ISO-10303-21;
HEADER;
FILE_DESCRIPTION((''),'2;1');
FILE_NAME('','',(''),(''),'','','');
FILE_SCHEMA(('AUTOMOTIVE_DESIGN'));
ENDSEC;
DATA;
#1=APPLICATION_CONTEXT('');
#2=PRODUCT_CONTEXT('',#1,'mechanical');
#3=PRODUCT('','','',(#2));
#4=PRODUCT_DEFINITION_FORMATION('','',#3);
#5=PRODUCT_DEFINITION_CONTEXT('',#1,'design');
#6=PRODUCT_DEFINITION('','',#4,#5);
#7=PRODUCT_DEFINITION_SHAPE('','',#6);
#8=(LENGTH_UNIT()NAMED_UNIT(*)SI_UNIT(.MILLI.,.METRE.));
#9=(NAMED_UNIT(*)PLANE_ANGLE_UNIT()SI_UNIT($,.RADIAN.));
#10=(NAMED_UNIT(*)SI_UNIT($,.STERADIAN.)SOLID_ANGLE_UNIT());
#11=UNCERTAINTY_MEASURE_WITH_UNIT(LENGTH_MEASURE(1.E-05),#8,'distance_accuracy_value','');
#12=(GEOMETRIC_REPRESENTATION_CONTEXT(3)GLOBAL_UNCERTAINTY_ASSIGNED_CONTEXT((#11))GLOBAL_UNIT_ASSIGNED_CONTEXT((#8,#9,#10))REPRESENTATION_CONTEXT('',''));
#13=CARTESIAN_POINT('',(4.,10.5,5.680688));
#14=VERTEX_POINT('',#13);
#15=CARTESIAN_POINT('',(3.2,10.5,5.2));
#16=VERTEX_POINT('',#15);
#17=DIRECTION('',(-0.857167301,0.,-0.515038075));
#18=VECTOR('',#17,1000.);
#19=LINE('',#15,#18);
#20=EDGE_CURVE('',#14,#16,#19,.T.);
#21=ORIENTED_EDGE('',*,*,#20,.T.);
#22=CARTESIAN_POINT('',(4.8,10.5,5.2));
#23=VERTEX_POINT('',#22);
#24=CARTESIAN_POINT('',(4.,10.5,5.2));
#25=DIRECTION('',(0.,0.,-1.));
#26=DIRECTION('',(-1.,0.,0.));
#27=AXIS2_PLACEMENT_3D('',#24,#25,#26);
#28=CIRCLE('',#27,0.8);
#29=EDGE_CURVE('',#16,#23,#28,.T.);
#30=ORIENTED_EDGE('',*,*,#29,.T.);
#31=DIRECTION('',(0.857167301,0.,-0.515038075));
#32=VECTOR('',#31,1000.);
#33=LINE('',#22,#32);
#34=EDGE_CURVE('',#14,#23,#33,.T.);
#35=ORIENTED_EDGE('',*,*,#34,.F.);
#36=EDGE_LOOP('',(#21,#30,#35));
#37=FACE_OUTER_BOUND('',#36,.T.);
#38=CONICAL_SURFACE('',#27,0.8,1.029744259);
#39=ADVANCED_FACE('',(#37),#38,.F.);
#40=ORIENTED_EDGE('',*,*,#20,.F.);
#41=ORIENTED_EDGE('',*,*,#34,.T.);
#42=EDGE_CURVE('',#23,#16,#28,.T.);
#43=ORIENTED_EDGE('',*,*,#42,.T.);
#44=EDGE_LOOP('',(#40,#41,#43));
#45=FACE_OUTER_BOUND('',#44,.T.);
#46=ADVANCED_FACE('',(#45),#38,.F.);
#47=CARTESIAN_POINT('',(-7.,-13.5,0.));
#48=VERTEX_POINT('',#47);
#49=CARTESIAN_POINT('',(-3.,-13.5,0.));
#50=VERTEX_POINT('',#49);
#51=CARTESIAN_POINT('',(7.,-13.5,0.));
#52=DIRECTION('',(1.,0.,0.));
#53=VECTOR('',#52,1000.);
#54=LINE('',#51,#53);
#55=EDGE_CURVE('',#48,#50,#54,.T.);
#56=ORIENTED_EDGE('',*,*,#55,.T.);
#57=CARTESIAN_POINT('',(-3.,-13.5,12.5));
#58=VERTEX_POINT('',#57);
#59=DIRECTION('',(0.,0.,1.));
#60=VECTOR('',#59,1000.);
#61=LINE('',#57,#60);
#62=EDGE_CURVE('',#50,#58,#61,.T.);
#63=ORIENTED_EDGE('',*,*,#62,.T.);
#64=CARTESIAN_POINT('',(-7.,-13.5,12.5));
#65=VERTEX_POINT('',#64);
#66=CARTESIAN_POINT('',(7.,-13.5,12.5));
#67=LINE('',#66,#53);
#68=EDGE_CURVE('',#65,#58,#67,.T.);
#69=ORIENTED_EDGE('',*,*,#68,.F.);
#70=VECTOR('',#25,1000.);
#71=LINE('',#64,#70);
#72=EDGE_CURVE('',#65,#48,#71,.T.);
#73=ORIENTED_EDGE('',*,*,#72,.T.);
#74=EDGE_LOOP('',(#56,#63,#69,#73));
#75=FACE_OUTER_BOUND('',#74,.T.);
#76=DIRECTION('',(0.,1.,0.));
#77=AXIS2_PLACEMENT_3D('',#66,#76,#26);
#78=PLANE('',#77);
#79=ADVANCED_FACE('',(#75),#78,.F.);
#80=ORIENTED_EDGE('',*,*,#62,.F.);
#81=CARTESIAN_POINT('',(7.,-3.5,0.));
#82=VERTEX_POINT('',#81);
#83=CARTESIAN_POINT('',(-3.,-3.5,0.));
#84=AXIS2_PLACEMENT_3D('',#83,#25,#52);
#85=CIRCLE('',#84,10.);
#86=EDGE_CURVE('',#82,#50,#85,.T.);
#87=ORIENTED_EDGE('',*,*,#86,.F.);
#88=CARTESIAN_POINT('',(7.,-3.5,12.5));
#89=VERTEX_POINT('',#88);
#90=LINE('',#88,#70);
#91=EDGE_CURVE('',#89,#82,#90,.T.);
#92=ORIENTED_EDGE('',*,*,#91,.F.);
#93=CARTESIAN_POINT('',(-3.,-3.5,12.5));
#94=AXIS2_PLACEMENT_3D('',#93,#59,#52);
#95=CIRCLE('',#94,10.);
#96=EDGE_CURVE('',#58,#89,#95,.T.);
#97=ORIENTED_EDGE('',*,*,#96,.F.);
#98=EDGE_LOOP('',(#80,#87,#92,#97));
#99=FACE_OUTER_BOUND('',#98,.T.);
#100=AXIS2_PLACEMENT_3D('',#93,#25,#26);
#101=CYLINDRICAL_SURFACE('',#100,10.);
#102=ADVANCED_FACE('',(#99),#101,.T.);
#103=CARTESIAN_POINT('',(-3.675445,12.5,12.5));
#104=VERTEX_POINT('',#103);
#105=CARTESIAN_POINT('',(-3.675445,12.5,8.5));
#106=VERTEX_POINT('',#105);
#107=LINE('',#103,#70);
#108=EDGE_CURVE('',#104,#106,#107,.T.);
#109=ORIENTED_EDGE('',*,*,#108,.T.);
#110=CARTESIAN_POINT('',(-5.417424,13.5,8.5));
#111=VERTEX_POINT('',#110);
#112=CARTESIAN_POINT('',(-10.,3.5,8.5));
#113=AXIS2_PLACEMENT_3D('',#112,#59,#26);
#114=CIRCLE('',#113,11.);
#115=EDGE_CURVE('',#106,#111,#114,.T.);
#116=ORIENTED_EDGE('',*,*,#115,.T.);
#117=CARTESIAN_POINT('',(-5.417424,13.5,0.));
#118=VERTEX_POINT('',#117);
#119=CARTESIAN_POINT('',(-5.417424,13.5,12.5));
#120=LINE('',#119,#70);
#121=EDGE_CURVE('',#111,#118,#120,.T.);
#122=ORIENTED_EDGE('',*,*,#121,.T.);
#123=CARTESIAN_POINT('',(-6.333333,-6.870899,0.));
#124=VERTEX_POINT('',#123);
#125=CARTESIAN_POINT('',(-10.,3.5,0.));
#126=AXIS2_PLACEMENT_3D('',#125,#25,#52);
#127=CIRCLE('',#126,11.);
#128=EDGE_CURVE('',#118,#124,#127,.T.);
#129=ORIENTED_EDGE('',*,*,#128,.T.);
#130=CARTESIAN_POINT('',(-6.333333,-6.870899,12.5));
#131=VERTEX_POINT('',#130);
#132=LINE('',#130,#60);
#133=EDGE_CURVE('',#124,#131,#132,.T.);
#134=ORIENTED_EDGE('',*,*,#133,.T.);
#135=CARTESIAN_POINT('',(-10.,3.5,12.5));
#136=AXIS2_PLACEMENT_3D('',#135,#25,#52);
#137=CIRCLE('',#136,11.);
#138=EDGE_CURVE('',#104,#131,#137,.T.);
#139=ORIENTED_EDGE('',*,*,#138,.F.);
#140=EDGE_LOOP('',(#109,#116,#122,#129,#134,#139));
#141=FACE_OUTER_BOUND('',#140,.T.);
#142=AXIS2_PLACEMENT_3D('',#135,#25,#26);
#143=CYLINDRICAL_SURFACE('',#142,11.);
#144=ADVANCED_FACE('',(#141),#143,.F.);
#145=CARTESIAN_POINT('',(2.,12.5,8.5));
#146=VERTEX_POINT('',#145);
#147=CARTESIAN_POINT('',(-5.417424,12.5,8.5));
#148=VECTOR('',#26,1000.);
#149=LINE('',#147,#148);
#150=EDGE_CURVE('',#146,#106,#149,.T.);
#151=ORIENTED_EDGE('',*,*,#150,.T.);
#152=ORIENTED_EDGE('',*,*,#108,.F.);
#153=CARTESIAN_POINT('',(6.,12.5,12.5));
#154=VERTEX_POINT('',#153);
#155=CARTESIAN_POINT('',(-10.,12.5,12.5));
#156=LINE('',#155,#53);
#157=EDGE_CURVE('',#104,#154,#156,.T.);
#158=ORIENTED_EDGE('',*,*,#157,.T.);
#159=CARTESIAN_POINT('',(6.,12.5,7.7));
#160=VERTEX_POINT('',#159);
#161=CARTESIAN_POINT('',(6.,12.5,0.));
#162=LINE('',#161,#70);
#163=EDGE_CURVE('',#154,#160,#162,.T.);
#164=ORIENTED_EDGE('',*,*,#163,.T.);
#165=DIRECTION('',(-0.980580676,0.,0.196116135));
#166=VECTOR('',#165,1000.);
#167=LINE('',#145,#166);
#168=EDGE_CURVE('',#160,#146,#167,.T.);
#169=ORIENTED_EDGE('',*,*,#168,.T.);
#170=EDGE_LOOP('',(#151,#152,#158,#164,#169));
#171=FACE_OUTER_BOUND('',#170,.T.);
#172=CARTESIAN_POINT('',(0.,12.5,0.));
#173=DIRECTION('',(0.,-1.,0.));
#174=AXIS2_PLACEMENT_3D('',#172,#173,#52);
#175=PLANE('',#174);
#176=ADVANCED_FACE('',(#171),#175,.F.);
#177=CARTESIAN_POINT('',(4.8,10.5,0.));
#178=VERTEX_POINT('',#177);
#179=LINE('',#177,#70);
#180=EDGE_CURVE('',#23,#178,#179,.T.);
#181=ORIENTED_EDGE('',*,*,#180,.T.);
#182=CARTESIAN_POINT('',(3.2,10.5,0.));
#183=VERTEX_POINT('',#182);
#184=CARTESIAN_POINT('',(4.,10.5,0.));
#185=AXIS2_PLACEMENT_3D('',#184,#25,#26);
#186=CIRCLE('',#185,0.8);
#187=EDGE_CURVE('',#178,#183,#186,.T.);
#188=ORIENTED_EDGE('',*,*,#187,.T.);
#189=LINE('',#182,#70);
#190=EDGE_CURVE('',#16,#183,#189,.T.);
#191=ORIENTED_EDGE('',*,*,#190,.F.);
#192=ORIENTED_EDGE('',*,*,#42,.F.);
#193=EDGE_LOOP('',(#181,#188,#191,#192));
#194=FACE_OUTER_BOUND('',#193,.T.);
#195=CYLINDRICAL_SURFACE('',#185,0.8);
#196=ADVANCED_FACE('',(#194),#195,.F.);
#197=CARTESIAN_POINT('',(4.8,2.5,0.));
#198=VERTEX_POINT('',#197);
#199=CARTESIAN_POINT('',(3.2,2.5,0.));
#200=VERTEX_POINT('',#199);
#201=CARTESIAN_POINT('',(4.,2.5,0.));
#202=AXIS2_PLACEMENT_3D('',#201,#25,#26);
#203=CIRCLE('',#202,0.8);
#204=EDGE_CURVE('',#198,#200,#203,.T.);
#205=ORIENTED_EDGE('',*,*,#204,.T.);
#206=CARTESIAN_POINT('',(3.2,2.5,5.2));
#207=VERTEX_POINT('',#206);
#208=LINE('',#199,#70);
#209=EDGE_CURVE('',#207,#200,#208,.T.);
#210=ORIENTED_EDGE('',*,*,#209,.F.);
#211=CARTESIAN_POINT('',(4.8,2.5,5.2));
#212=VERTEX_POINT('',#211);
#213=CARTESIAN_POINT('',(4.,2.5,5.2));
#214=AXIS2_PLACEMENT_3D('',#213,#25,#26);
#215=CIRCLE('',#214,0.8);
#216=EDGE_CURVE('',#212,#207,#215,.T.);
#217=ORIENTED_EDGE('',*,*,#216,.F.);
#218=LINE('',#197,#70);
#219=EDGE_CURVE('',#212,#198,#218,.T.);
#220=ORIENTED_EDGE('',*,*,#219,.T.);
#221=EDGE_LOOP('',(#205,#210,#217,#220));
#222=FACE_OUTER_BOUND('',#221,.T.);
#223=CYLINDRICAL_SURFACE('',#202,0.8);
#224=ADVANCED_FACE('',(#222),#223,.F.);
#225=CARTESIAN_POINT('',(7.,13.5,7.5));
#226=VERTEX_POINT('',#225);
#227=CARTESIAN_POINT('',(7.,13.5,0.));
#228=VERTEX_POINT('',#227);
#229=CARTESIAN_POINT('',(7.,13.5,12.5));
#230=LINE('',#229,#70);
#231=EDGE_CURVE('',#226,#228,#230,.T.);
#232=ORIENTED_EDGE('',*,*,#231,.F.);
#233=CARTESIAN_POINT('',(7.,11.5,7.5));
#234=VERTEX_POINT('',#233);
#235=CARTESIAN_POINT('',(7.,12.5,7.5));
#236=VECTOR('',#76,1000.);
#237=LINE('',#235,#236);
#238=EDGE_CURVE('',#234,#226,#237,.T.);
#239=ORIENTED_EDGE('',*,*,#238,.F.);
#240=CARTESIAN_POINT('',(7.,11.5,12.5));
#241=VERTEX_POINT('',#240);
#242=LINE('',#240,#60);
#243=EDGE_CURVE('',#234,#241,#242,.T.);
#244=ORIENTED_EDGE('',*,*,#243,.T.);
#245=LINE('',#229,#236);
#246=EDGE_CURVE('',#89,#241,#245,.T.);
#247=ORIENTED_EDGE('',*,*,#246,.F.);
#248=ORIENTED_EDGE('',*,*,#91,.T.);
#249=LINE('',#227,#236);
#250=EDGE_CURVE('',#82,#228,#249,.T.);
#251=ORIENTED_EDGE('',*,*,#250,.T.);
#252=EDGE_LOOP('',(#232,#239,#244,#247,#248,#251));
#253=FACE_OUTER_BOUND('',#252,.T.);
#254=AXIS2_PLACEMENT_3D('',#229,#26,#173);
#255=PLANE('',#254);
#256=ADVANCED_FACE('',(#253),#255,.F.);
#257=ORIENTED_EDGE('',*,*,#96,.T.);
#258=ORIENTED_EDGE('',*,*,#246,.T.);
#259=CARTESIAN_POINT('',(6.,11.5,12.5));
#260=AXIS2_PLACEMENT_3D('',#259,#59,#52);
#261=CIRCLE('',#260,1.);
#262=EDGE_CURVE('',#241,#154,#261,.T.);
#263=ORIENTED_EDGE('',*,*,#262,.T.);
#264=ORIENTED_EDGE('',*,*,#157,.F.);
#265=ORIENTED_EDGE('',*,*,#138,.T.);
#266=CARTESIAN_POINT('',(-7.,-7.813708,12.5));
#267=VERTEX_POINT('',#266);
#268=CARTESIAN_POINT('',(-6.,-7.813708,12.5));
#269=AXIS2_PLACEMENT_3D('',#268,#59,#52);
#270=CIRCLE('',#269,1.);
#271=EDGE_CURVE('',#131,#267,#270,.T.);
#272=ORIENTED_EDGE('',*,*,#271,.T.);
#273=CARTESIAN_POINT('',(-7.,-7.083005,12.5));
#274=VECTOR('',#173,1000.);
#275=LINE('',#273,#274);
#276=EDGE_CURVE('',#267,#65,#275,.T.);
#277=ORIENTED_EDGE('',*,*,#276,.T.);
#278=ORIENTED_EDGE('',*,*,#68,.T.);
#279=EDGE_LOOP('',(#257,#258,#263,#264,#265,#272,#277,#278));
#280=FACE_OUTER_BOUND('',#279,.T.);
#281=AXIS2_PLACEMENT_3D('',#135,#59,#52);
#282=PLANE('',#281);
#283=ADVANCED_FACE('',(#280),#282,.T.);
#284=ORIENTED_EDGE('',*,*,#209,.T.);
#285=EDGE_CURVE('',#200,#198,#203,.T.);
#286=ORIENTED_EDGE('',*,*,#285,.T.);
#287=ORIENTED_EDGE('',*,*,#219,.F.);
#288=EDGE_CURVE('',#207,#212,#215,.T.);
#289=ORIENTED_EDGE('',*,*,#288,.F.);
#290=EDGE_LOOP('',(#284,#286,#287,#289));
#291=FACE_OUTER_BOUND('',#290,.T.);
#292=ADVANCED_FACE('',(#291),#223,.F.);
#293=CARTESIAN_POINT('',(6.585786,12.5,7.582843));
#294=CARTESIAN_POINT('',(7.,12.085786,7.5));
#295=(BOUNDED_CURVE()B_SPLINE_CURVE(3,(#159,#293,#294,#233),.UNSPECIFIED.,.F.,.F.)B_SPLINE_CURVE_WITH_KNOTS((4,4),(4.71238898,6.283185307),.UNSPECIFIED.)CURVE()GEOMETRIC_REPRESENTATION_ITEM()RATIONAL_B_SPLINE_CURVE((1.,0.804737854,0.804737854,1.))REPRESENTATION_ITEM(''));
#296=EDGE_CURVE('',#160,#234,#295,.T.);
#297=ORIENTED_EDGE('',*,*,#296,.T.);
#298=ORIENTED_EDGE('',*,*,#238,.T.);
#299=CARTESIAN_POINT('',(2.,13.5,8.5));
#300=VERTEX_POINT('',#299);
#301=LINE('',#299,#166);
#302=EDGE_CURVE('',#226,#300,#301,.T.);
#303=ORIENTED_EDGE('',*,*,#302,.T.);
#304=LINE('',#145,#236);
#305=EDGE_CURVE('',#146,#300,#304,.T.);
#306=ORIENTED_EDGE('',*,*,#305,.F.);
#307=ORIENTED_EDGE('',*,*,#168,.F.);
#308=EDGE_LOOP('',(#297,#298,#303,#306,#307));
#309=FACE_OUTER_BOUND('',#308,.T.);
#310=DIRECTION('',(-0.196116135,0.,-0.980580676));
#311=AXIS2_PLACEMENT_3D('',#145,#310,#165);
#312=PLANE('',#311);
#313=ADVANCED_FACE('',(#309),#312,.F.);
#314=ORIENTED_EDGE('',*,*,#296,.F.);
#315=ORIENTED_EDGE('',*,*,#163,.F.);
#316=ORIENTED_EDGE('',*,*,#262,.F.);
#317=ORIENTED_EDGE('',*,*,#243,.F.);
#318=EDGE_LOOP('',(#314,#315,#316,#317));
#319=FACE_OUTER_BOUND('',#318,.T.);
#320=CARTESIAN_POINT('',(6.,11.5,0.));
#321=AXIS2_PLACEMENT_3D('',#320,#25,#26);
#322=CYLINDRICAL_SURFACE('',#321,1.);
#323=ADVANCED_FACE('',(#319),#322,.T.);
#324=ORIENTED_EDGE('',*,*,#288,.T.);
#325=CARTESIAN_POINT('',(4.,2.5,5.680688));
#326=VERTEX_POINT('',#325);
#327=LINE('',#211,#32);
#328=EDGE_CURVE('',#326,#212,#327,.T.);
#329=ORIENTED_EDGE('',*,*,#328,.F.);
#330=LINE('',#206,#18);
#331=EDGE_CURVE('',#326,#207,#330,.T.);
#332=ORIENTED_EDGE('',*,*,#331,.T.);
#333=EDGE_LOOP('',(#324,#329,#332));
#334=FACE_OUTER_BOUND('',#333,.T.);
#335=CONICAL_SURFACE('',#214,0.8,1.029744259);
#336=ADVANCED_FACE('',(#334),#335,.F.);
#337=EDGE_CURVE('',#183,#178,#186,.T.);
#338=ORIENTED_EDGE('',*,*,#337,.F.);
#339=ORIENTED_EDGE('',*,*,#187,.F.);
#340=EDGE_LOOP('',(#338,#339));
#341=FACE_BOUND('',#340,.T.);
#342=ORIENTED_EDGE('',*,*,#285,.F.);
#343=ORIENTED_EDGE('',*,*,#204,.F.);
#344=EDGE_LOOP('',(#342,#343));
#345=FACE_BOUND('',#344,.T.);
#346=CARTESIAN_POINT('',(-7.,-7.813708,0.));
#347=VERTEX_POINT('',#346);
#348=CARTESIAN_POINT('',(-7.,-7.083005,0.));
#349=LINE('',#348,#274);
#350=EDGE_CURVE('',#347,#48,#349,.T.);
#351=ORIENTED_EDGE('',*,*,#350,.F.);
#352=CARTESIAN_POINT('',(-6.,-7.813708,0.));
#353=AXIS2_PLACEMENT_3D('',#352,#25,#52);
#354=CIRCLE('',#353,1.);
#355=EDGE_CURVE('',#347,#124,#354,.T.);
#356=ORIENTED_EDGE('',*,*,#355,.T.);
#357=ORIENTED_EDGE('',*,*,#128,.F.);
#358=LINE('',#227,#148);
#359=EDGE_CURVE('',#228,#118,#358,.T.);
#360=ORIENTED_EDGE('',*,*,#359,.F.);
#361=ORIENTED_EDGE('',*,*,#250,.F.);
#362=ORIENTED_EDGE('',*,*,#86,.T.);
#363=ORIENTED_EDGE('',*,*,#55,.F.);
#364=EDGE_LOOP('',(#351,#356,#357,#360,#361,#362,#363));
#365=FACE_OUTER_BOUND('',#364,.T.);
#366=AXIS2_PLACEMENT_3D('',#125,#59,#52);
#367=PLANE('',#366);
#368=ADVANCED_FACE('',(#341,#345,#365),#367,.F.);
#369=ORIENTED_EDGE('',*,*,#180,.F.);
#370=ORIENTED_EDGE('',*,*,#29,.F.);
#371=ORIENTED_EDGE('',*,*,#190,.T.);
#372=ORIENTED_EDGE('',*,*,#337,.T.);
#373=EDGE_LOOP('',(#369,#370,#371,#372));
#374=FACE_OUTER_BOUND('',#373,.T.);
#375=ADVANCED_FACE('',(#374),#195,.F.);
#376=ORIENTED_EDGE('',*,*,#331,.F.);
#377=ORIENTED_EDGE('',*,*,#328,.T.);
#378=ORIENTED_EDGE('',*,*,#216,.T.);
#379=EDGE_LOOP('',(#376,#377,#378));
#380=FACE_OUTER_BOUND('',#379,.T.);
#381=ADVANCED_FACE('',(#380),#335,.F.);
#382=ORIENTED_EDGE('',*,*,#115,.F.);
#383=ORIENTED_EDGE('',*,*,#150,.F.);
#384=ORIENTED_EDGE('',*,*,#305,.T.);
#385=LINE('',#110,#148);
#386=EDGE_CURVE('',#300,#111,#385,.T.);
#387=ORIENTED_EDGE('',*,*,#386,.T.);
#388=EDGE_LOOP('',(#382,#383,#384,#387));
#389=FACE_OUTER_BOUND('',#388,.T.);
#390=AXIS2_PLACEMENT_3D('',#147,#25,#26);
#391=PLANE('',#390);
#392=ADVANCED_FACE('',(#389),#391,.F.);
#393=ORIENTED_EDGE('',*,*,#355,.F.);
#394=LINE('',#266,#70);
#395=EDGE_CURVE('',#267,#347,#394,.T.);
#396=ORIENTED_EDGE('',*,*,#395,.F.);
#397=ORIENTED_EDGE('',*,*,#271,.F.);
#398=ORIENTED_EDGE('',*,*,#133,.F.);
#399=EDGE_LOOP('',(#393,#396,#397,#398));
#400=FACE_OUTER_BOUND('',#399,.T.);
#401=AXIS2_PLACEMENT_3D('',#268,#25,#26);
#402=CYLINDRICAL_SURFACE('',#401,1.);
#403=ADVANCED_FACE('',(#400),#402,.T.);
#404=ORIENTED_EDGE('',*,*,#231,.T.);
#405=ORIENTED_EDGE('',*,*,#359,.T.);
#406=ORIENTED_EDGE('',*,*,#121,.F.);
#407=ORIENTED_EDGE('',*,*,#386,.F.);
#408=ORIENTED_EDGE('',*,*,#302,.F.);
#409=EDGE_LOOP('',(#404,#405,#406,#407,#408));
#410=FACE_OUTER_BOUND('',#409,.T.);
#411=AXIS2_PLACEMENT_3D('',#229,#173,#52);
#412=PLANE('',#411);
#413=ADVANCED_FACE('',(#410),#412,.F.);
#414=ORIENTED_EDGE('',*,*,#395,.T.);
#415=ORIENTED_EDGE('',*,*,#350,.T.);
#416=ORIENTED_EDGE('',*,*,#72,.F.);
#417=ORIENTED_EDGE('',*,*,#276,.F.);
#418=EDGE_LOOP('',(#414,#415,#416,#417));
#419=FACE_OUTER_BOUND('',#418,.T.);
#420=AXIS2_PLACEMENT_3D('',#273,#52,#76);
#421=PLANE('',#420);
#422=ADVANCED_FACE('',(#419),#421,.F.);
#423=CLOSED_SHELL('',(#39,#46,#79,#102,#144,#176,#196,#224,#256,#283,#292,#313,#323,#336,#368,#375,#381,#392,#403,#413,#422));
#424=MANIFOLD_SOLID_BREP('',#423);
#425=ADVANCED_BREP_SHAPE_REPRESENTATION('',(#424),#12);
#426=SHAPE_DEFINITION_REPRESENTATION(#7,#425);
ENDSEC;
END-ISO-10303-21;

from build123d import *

# Parameters (mm, degrees)
EXTRUDE_1_DEPTH        = 12.5
CUT_EXTRUDE_1_DEPTH    = 1
FILLET_1_R             = 10
FILLET_2_R             = 1
HOLE_WIZARD_M2_1_D     = 1.6
HOLE_WIZARD_M2_1_DEPTH = 5.2
HOLE_WIZARD_M2_1_TIP   = 0.480688495
FILLET_4_R             = 1


with BuildPart() as part:
    # 草图1 → 凸台-拉伸1 (new body)
    with BuildSketch(Plane.XY):
        with BuildLine():
            Line((-7, -7.083005244), (-7, -13.5))
            Line((-7, -13.5), (7, -13.5))
            Line((7, -13.5), (7, 13.5))
            Line((7, 13.5), (-5.417424305, 13.5))
            ThreePointArc((-5.417424305, 13.5), (0.967629177, 2.656726476), (-7, -7.083005244))
        make_face()
    extrude(amount=EXTRUDE_1_DEPTH)

    # 草图2 → 切除-拉伸1 (cut)
    with BuildSketch(Plane(origin=(0, 13.5, 0), x_dir=(1, 0, 0), z_dir=(0, 1, 0))):
        Polygon((-5.417424305, -12.5), (-5.417424305, -8.5), (2, -8.5), (7, -7.5), (7, -12.5), align=None)
    extrude(amount=-CUT_EXTRUDE_1_DEPTH, mode=Mode.SUBTRACT)

    # 圆角1
    fillet_1_edges = [part.edges().sort_by_distance(p)[0] for p in [
        (7, -13.5, 6.25),
    ]]
    fillet(fillet_1_edges, radius=FILLET_1_R)

    # 圆角2
    fillet_2_edges = [part.edges().sort_by_distance(p)[0] for p in [
        (7, 12.5, 10),
    ]]
    fillet(fillet_2_edges, radius=FILLET_2_R)

    # M2 螺纹孔1
    with Locations(Plane(origin=(0, 0, 0), x_dir=(-1, 0, 0), z_dir=(0, 0, -1))):
        with Locations((-4, 2.5), (-4, 10.5)):
            Hole(HOLE_WIZARD_M2_1_D / 2, depth=HOLE_WIZARD_M2_1_DEPTH)
            with Locations((0, 0, -(HOLE_WIZARD_M2_1_DEPTH + HOLE_WIZARD_M2_1_TIP / 2))):  # 118° drill point
                Cone(0, HOLE_WIZARD_M2_1_D / 2, HOLE_WIZARD_M2_1_TIP, mode=Mode.SUBTRACT)

    # 圆角4
    fillet_4_edges = [part.edges().sort_by_distance(p)[0] for p in [
        (-7, -7.083005244, 6.25),
    ]]
    fillet(fillet_4_edges, radius=FILLET_4_R)


solid = part.part
